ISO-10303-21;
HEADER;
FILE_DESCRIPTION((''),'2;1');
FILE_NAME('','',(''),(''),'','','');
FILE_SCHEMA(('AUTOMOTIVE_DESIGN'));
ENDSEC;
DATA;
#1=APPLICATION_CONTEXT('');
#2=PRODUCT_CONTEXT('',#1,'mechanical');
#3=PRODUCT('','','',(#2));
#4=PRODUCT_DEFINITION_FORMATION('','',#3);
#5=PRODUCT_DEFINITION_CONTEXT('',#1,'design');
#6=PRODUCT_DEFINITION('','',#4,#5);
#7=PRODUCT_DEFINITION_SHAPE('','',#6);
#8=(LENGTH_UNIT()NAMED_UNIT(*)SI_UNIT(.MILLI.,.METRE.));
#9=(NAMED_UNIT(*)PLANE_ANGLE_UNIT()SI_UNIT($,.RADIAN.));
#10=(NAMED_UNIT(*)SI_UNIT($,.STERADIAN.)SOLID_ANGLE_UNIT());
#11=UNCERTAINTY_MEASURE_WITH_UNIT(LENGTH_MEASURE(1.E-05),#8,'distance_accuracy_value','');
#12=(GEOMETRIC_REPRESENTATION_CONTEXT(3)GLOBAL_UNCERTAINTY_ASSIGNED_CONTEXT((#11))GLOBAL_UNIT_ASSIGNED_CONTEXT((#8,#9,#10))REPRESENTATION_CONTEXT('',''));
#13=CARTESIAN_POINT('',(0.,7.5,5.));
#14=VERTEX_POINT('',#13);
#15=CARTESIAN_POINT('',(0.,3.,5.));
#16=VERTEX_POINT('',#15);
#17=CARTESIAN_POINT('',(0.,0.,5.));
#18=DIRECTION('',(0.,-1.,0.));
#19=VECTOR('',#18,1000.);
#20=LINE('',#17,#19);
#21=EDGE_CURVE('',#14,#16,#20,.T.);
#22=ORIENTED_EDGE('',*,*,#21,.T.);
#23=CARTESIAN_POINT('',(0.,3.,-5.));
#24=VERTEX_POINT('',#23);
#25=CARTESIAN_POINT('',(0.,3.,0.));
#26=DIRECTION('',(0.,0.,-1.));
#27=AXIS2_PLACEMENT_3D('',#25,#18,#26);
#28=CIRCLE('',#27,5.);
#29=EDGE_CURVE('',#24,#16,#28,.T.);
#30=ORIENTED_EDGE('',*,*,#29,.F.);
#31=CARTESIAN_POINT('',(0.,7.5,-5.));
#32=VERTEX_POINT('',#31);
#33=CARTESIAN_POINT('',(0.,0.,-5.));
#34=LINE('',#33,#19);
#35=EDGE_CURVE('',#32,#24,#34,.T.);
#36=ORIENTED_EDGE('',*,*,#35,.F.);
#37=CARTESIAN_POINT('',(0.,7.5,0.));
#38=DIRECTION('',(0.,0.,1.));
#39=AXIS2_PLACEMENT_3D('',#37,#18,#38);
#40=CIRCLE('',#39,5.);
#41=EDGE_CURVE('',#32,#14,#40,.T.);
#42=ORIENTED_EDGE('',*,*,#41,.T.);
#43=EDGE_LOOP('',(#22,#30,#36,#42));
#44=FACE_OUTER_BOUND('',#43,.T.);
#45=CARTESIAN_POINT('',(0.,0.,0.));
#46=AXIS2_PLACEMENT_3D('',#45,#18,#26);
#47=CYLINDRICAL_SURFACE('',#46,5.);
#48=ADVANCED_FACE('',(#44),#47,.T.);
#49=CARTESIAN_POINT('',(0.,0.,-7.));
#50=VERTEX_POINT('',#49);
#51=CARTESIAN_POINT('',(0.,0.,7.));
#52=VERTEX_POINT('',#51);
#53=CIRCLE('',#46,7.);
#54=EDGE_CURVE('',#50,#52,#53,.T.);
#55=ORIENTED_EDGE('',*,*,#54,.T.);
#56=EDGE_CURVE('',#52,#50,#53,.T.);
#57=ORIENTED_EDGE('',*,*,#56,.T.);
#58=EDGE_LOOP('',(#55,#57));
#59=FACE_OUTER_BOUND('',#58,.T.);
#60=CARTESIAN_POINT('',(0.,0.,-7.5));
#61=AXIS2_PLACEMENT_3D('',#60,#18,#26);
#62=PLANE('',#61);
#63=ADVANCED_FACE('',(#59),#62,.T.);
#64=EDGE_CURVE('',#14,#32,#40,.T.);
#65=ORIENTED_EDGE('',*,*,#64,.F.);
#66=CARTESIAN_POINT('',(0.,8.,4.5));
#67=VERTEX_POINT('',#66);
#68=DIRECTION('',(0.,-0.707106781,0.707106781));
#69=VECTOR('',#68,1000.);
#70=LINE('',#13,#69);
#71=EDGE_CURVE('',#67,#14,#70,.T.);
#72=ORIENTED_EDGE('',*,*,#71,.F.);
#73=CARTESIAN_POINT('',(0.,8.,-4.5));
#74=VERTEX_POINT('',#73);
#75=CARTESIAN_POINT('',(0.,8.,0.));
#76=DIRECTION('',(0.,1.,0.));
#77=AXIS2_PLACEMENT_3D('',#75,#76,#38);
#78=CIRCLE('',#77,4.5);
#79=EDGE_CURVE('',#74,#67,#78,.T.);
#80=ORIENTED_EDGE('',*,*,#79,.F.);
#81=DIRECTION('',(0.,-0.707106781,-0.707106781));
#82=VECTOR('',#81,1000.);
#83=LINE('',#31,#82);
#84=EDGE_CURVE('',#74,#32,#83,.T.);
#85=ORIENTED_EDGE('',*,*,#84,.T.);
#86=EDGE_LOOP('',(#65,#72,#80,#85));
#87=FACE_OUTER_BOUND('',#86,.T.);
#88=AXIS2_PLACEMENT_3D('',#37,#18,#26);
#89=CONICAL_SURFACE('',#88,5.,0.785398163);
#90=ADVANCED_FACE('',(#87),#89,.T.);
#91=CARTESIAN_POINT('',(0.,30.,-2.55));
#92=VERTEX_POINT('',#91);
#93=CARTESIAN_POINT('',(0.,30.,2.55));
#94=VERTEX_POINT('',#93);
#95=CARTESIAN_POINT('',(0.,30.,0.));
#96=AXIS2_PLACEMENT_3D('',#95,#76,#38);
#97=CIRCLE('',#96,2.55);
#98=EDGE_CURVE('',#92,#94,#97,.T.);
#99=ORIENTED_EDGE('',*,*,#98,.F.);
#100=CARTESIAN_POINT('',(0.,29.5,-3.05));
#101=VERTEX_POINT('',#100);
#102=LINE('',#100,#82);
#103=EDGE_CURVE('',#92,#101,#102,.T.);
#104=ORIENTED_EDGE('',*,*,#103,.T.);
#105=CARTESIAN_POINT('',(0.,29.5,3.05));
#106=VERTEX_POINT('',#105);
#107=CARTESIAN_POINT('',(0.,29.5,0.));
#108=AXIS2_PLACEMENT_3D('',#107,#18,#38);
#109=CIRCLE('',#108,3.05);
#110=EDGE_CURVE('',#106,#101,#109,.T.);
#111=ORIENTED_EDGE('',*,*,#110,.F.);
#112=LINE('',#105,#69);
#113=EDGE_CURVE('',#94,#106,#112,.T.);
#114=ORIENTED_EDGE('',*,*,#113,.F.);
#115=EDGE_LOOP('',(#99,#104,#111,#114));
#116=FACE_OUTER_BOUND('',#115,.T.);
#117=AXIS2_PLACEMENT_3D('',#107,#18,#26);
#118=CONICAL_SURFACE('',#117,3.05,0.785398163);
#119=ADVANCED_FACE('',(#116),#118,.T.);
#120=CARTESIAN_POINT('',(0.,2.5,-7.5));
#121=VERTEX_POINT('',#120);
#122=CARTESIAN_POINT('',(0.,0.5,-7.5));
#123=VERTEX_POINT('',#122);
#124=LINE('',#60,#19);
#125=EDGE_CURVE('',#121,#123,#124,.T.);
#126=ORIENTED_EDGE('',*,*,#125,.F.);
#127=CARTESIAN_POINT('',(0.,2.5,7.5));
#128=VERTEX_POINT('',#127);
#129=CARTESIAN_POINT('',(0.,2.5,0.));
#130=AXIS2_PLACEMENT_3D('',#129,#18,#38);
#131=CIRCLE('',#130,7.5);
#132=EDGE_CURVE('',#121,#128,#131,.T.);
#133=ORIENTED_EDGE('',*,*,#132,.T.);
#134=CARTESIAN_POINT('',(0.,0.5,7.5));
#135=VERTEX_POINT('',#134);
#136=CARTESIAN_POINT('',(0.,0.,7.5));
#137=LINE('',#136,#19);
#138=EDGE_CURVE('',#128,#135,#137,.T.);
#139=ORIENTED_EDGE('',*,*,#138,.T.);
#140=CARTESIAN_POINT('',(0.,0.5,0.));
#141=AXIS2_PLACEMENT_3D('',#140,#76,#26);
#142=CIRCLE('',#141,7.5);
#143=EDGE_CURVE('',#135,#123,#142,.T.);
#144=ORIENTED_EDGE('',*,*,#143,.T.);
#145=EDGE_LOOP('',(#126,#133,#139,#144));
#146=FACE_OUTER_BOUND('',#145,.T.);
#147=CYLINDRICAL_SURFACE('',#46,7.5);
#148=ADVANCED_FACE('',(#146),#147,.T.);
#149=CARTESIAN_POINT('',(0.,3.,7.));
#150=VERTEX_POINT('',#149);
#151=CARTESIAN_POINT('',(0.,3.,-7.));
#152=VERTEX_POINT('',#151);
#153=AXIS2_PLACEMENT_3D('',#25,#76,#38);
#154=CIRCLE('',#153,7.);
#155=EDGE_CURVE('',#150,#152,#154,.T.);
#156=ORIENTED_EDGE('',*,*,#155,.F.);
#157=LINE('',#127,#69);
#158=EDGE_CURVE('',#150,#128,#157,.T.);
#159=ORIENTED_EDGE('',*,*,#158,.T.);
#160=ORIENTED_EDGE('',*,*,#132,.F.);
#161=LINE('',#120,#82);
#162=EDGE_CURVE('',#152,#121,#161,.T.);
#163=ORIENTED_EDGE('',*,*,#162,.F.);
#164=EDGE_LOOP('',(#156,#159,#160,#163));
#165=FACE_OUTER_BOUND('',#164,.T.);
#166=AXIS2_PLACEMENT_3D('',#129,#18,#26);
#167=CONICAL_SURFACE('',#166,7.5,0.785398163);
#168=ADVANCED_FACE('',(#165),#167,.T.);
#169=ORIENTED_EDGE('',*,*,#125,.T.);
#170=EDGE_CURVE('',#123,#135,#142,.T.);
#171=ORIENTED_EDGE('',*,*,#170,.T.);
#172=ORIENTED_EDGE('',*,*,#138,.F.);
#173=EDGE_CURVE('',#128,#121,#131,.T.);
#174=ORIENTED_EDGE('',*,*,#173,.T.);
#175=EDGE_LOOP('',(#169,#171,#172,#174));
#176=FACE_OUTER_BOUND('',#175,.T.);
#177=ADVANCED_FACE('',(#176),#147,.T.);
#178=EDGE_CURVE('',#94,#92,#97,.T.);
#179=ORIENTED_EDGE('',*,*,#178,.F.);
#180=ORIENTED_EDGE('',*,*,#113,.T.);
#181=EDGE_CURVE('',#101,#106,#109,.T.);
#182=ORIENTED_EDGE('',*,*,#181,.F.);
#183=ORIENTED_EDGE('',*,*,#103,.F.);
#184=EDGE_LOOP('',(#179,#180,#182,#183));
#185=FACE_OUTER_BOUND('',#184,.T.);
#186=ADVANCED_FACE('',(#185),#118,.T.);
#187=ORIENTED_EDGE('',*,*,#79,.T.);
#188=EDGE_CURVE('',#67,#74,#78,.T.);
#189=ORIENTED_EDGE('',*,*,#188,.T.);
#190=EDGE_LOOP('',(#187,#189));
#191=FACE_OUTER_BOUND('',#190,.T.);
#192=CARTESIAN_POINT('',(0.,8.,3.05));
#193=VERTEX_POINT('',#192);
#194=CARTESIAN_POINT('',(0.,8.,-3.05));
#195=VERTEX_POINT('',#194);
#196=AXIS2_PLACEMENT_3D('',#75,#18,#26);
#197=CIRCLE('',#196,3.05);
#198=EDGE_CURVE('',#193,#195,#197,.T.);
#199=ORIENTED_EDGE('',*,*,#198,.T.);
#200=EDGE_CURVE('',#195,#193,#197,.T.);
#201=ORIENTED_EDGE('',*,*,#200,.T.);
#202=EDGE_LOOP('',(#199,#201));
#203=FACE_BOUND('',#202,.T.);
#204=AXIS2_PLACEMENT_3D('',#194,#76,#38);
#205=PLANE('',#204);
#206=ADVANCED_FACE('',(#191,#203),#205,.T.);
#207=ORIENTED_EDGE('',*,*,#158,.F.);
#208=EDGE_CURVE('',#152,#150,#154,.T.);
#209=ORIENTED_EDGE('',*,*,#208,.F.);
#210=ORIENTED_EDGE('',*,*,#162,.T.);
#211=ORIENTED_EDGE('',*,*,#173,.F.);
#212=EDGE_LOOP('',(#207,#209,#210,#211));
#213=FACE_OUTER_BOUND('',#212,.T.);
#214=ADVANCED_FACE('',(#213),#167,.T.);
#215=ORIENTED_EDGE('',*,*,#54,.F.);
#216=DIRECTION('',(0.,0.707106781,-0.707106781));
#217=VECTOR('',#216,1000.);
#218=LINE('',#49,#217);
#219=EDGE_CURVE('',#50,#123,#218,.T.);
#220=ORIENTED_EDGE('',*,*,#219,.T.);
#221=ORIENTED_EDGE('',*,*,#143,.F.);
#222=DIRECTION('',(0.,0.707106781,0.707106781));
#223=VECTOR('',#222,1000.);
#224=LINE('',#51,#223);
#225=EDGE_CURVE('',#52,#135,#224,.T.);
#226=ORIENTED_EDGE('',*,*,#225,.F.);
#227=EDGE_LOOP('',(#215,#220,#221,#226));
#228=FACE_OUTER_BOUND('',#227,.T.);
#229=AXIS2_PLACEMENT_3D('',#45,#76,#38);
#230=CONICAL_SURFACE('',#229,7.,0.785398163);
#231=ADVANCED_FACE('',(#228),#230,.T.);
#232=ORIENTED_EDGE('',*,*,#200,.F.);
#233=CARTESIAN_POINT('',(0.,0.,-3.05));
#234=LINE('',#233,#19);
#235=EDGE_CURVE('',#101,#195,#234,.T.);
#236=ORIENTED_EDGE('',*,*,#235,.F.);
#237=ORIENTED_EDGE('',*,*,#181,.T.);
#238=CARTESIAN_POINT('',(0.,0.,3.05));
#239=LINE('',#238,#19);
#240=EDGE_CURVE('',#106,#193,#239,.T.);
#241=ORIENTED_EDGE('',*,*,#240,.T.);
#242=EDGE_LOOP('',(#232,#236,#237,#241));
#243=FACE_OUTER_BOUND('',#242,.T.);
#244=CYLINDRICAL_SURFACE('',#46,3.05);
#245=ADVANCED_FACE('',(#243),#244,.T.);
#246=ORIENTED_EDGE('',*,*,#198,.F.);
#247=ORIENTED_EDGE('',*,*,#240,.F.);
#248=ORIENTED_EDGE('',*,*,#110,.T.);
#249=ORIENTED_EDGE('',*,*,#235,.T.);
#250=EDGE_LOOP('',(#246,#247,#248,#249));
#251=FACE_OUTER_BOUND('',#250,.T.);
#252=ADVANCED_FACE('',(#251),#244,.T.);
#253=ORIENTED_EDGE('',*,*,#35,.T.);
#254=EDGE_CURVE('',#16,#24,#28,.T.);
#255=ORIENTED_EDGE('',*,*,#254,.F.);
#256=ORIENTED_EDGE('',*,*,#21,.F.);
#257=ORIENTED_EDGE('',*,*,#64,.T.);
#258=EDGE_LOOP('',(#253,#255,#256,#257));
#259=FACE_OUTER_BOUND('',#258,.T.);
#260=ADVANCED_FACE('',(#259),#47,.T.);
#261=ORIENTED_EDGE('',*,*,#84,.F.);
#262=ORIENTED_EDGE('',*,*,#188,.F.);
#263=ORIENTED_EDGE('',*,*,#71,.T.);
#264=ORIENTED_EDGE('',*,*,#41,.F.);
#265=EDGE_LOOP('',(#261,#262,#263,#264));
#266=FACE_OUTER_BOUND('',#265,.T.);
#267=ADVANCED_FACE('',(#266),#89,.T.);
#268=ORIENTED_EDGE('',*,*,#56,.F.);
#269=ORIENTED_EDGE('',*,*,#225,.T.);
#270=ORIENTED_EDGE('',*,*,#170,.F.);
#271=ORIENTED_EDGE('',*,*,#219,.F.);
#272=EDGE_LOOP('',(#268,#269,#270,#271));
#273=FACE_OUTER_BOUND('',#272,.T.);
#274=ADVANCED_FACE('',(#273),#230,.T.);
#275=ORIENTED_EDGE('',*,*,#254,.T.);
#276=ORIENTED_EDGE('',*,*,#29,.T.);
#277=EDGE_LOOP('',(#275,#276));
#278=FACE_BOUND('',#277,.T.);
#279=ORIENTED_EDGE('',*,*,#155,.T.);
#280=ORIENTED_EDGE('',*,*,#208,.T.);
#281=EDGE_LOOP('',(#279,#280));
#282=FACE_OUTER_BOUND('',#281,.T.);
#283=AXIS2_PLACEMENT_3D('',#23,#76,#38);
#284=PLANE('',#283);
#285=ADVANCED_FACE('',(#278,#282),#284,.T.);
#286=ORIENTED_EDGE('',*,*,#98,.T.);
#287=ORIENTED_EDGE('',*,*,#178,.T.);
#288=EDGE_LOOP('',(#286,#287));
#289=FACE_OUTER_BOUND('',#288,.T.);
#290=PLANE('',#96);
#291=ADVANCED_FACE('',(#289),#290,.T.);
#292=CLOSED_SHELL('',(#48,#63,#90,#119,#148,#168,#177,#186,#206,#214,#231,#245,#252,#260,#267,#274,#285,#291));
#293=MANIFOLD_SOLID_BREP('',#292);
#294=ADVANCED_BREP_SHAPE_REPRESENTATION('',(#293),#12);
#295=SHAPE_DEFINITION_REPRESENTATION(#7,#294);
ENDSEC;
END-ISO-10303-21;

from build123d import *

# Parameters (mm, degrees)
CHAMFER1_SIZE = 0.5


with BuildPart() as part:
    # Sketch1 → Revolve1 (revolve)
    with BuildSketch(Plane(origin=(0, 0, 0), x_dir=(0, 0, -1), z_dir=(1, 0, 0))):
        Polygon((0, 30), (3.05, 30), (3.05, 8), (5, 8), (5, 3), (7.5, 3), (7.5, 0), (0, 0), align=None)
    revolve(axis=Axis((0, 0, 0), (0, 1, 0)))

    # Chamfer1
    chamfer1_edges = [part.edges().sort_by_distance(p)[0] for p in [
        (0, 0, 7.5),
        (0, 3, 7.5),
        (0, 8, 5),
        (0, 30, 3.05),
    ]]
    chamfer(chamfer1_edges, length=CHAMFER1_SIZE)


solid = part.part
